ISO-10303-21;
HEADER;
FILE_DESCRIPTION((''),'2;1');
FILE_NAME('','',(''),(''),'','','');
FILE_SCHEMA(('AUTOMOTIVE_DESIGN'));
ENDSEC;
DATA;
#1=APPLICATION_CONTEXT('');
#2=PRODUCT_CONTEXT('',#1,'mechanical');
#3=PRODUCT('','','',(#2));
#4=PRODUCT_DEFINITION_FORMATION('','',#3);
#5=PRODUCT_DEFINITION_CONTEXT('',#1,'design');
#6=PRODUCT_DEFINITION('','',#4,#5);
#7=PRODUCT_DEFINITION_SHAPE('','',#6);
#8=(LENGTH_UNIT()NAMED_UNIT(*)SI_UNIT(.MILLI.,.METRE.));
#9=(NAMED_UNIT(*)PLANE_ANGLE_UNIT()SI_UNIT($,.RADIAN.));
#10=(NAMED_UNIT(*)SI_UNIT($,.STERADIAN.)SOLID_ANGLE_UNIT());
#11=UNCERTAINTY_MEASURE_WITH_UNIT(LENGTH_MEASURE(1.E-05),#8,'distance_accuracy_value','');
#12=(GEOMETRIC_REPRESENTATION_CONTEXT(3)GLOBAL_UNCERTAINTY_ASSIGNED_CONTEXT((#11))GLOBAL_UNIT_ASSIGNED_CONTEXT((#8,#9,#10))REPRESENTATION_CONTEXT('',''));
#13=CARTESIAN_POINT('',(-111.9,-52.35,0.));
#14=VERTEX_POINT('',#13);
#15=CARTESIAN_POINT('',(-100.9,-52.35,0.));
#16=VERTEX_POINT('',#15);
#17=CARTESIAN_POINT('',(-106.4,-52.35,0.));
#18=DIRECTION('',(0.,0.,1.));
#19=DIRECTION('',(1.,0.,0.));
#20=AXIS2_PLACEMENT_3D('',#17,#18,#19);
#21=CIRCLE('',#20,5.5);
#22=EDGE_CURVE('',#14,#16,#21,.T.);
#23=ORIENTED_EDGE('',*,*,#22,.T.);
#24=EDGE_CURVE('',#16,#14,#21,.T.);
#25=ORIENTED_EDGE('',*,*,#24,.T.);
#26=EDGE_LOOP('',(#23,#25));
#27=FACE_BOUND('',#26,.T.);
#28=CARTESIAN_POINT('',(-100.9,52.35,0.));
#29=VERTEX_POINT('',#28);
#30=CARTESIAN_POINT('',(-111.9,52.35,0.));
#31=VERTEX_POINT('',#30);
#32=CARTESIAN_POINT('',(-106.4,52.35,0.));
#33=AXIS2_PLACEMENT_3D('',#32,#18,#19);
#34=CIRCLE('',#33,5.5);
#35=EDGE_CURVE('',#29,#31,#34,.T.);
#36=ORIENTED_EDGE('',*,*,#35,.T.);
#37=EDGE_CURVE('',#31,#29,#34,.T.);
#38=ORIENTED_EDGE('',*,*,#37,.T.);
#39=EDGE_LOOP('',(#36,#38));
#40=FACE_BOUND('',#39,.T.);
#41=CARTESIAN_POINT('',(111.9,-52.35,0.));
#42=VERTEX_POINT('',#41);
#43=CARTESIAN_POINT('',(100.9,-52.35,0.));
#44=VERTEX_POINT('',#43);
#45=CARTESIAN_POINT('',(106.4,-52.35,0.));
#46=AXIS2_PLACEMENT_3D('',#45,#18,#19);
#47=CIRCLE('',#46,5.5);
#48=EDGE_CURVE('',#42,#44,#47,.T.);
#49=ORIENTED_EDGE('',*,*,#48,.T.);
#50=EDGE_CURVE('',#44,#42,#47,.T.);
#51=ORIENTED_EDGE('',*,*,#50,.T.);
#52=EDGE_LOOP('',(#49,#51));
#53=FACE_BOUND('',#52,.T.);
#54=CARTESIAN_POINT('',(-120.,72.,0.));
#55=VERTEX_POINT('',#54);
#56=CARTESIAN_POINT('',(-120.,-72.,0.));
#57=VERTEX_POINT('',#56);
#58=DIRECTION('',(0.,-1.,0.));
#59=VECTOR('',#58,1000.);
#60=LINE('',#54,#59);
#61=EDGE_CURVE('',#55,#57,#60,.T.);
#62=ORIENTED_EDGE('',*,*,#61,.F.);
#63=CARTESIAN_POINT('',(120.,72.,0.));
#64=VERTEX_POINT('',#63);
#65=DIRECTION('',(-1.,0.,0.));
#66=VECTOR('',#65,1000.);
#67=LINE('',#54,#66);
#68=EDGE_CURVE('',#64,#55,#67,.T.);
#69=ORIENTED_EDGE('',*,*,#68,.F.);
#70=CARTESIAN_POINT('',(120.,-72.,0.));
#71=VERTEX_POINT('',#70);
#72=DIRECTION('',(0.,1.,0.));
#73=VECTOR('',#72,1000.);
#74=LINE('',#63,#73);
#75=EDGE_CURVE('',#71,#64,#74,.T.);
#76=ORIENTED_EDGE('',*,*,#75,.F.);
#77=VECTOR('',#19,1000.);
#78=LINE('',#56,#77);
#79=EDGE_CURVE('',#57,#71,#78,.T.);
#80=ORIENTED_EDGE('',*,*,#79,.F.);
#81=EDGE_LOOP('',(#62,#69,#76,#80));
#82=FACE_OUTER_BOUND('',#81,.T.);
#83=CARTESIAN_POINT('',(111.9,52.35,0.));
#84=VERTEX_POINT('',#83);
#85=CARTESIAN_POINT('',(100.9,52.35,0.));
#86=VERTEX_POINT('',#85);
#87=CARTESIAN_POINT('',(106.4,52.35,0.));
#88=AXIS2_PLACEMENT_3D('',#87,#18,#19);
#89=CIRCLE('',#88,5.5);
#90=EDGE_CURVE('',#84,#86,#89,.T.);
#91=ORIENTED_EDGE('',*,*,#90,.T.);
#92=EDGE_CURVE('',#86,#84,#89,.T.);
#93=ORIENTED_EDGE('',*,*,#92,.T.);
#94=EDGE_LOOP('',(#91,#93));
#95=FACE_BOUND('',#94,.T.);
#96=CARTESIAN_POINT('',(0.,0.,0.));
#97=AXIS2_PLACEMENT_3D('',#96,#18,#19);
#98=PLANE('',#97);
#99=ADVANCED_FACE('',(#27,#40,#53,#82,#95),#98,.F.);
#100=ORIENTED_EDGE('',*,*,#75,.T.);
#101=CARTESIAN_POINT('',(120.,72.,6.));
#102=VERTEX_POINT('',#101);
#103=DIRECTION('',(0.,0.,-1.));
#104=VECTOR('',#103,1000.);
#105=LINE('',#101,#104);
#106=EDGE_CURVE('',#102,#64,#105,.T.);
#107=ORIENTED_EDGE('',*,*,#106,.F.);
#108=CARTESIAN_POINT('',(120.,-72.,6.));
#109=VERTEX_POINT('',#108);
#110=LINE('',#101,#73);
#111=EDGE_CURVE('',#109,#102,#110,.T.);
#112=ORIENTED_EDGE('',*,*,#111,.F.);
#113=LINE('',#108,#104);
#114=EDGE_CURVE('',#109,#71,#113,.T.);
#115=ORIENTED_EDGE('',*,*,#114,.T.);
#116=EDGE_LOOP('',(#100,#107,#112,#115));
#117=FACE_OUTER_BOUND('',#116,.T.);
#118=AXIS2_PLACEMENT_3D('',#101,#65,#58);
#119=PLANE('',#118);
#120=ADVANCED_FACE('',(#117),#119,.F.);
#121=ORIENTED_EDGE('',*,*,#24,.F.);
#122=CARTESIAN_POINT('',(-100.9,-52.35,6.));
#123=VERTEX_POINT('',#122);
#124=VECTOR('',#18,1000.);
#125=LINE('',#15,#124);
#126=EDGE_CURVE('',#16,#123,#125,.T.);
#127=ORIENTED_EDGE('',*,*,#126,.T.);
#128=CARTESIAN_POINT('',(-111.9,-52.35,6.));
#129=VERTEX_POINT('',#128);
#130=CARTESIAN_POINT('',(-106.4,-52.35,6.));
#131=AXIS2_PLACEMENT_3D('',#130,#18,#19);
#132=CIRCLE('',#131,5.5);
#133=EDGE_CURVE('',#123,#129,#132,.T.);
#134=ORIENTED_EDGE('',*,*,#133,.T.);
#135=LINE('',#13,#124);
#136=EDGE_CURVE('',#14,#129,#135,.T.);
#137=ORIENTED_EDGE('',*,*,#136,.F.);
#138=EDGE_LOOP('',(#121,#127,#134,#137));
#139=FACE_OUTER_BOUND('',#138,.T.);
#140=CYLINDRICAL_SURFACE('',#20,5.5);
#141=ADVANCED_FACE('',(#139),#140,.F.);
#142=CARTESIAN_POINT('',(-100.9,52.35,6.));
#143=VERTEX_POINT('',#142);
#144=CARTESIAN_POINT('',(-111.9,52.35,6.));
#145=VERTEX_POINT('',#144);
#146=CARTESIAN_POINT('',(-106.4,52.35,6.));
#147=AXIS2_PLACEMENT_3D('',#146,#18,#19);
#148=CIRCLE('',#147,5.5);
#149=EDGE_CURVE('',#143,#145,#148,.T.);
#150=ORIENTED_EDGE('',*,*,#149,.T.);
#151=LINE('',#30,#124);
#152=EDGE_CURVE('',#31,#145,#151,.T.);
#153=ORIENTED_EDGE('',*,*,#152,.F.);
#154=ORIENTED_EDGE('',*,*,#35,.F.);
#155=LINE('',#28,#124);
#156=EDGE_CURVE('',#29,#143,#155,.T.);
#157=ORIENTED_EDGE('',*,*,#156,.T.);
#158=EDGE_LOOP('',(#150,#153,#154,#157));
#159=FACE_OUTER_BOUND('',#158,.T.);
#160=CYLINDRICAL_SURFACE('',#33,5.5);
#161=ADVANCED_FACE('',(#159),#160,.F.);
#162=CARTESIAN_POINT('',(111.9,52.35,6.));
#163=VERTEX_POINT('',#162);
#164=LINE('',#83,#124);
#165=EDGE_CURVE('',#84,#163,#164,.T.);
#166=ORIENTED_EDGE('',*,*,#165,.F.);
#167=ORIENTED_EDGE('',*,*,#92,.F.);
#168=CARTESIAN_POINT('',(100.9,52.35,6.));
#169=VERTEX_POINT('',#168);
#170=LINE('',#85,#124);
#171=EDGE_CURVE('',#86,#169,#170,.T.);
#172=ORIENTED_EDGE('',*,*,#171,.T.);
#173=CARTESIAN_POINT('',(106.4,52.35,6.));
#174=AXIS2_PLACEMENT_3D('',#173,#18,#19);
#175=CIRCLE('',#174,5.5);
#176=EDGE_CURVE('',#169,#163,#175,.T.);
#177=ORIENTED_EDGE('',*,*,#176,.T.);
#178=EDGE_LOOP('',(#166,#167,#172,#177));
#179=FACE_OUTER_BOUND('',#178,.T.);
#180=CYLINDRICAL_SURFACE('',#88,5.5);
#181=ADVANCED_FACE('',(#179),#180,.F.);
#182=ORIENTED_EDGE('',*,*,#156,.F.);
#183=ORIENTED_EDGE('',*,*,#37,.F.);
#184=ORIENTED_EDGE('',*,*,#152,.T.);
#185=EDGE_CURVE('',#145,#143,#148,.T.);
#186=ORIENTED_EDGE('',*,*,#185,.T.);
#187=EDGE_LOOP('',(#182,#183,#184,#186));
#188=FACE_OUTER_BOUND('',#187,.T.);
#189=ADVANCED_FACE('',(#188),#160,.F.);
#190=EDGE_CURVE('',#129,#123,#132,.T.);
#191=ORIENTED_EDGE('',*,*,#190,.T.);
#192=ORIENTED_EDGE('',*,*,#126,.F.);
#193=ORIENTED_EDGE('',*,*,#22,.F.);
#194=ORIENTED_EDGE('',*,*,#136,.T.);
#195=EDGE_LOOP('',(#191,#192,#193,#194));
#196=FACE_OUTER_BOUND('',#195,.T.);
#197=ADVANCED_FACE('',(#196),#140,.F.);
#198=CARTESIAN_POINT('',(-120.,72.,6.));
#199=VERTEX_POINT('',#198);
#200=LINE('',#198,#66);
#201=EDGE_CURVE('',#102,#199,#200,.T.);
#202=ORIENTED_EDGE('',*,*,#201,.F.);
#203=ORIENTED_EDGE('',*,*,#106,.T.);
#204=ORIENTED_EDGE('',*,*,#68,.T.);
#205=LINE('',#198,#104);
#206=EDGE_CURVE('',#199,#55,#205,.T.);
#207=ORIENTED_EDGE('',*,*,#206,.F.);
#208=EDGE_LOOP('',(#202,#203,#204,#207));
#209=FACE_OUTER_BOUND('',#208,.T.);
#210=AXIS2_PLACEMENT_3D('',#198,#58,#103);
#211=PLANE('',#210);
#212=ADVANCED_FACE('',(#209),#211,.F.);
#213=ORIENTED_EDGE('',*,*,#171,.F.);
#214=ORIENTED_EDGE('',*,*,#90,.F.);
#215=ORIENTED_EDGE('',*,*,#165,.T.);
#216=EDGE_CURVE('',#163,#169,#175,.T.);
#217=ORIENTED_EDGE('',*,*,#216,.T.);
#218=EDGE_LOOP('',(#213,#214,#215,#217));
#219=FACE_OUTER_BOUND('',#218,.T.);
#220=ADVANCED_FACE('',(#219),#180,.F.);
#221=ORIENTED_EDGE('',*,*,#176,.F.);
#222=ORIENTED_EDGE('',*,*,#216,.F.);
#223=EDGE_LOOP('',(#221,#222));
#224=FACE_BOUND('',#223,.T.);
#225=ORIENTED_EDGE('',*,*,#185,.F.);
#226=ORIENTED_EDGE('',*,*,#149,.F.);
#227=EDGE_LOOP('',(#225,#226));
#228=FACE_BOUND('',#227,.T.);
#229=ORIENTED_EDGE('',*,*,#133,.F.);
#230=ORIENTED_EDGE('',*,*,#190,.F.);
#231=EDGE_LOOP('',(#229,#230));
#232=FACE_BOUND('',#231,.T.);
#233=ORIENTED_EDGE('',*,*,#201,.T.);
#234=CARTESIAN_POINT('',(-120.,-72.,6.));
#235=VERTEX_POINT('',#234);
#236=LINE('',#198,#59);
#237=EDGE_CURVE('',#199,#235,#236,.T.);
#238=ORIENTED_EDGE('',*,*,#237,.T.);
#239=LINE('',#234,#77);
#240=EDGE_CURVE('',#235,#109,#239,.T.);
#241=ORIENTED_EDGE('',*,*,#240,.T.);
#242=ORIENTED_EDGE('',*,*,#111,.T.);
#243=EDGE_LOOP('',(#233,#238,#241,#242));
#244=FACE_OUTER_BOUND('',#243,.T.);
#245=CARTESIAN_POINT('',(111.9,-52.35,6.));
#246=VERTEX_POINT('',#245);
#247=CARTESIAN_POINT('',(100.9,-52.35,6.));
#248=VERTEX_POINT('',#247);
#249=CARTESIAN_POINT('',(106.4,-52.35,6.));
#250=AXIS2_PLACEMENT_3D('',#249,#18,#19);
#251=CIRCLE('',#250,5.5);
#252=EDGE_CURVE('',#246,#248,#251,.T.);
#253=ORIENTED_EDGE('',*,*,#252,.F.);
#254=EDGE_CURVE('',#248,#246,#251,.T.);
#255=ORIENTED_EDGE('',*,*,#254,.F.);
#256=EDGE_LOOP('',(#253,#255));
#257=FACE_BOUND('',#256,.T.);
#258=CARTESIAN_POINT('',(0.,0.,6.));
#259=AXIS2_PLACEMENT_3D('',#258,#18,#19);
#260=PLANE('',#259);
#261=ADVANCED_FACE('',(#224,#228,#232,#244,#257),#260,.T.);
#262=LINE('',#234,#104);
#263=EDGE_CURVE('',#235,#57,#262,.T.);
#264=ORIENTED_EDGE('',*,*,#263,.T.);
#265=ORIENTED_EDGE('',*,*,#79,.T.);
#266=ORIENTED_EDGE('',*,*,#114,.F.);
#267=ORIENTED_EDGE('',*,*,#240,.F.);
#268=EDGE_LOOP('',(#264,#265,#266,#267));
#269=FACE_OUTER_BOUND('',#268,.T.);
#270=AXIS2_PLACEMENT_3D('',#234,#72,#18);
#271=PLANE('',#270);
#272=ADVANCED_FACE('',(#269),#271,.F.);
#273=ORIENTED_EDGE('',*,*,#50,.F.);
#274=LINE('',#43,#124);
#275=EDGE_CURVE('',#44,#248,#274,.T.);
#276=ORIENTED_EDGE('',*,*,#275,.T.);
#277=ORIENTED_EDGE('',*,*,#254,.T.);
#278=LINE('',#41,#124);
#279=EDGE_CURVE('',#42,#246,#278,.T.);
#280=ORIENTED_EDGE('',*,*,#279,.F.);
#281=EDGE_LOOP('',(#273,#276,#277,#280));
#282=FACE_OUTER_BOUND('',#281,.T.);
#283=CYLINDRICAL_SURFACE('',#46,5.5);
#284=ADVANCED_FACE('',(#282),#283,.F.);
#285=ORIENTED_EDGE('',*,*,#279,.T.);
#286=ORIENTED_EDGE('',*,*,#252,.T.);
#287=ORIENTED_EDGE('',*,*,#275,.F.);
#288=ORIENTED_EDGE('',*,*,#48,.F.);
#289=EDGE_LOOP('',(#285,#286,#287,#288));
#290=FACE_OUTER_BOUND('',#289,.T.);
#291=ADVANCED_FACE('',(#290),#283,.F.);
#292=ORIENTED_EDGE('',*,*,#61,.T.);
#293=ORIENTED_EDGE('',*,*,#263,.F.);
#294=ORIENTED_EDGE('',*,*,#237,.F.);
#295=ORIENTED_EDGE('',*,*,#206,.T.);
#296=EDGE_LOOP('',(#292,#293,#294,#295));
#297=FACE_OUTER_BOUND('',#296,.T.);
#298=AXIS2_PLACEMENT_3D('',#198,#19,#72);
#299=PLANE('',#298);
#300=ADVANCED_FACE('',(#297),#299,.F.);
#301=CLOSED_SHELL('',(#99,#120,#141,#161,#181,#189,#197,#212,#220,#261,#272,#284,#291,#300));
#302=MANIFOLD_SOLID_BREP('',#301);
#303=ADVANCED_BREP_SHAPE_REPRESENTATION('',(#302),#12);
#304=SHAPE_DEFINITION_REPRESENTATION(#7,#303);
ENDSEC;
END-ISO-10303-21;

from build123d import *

# Parameters (mm, degrees)
SKETCH1_W            = 240
SKETCH1_H            = 144
BOSS_EXTRUDE1_DEPTH  = 6
SKETCH2_R            = 5.5
CUT_EXTRUDE1_DEPTH   = 6
LPATTERN1_COUNT      = 2
LPATTERN1_PITCH      = 212.8
LPATTERN1_COUNT_DIR2 = 2
LPATTERN1_PITCH_DIR2 = 104.7


with BuildPart() as part:
    # Sketch1 → Boss-Extrude1 (new body)
    with BuildSketch(Plane.XY):
        Rectangle(SKETCH1_W, SKETCH1_H)
    extrude(amount=BOSS_EXTRUDE1_DEPTH)

    # Sketch2 → Cut-Extrude1 (cut)
    with BuildSketch(Plane.XY.offset(6)):
        with Locations((-106.4, 52.35)):
            Circle(SKETCH2_R)
    cut_extrude1 = extrude(amount=-CUT_EXTRUDE1_DEPTH, mode=Mode.SUBTRACT)

    # LPattern1: Cut-Extrude1 2 × 2
    with Locations(*[(i * LPATTERN1_PITCH, -j * LPATTERN1_PITCH_DIR2, 0) for i in range(LPATTERN1_COUNT) for j in range(LPATTERN1_COUNT_DIR2) if (i, j) != (0, 0)]):
        add(cut_extrude1, mode=Mode.SUBTRACT)


solid = part.part
